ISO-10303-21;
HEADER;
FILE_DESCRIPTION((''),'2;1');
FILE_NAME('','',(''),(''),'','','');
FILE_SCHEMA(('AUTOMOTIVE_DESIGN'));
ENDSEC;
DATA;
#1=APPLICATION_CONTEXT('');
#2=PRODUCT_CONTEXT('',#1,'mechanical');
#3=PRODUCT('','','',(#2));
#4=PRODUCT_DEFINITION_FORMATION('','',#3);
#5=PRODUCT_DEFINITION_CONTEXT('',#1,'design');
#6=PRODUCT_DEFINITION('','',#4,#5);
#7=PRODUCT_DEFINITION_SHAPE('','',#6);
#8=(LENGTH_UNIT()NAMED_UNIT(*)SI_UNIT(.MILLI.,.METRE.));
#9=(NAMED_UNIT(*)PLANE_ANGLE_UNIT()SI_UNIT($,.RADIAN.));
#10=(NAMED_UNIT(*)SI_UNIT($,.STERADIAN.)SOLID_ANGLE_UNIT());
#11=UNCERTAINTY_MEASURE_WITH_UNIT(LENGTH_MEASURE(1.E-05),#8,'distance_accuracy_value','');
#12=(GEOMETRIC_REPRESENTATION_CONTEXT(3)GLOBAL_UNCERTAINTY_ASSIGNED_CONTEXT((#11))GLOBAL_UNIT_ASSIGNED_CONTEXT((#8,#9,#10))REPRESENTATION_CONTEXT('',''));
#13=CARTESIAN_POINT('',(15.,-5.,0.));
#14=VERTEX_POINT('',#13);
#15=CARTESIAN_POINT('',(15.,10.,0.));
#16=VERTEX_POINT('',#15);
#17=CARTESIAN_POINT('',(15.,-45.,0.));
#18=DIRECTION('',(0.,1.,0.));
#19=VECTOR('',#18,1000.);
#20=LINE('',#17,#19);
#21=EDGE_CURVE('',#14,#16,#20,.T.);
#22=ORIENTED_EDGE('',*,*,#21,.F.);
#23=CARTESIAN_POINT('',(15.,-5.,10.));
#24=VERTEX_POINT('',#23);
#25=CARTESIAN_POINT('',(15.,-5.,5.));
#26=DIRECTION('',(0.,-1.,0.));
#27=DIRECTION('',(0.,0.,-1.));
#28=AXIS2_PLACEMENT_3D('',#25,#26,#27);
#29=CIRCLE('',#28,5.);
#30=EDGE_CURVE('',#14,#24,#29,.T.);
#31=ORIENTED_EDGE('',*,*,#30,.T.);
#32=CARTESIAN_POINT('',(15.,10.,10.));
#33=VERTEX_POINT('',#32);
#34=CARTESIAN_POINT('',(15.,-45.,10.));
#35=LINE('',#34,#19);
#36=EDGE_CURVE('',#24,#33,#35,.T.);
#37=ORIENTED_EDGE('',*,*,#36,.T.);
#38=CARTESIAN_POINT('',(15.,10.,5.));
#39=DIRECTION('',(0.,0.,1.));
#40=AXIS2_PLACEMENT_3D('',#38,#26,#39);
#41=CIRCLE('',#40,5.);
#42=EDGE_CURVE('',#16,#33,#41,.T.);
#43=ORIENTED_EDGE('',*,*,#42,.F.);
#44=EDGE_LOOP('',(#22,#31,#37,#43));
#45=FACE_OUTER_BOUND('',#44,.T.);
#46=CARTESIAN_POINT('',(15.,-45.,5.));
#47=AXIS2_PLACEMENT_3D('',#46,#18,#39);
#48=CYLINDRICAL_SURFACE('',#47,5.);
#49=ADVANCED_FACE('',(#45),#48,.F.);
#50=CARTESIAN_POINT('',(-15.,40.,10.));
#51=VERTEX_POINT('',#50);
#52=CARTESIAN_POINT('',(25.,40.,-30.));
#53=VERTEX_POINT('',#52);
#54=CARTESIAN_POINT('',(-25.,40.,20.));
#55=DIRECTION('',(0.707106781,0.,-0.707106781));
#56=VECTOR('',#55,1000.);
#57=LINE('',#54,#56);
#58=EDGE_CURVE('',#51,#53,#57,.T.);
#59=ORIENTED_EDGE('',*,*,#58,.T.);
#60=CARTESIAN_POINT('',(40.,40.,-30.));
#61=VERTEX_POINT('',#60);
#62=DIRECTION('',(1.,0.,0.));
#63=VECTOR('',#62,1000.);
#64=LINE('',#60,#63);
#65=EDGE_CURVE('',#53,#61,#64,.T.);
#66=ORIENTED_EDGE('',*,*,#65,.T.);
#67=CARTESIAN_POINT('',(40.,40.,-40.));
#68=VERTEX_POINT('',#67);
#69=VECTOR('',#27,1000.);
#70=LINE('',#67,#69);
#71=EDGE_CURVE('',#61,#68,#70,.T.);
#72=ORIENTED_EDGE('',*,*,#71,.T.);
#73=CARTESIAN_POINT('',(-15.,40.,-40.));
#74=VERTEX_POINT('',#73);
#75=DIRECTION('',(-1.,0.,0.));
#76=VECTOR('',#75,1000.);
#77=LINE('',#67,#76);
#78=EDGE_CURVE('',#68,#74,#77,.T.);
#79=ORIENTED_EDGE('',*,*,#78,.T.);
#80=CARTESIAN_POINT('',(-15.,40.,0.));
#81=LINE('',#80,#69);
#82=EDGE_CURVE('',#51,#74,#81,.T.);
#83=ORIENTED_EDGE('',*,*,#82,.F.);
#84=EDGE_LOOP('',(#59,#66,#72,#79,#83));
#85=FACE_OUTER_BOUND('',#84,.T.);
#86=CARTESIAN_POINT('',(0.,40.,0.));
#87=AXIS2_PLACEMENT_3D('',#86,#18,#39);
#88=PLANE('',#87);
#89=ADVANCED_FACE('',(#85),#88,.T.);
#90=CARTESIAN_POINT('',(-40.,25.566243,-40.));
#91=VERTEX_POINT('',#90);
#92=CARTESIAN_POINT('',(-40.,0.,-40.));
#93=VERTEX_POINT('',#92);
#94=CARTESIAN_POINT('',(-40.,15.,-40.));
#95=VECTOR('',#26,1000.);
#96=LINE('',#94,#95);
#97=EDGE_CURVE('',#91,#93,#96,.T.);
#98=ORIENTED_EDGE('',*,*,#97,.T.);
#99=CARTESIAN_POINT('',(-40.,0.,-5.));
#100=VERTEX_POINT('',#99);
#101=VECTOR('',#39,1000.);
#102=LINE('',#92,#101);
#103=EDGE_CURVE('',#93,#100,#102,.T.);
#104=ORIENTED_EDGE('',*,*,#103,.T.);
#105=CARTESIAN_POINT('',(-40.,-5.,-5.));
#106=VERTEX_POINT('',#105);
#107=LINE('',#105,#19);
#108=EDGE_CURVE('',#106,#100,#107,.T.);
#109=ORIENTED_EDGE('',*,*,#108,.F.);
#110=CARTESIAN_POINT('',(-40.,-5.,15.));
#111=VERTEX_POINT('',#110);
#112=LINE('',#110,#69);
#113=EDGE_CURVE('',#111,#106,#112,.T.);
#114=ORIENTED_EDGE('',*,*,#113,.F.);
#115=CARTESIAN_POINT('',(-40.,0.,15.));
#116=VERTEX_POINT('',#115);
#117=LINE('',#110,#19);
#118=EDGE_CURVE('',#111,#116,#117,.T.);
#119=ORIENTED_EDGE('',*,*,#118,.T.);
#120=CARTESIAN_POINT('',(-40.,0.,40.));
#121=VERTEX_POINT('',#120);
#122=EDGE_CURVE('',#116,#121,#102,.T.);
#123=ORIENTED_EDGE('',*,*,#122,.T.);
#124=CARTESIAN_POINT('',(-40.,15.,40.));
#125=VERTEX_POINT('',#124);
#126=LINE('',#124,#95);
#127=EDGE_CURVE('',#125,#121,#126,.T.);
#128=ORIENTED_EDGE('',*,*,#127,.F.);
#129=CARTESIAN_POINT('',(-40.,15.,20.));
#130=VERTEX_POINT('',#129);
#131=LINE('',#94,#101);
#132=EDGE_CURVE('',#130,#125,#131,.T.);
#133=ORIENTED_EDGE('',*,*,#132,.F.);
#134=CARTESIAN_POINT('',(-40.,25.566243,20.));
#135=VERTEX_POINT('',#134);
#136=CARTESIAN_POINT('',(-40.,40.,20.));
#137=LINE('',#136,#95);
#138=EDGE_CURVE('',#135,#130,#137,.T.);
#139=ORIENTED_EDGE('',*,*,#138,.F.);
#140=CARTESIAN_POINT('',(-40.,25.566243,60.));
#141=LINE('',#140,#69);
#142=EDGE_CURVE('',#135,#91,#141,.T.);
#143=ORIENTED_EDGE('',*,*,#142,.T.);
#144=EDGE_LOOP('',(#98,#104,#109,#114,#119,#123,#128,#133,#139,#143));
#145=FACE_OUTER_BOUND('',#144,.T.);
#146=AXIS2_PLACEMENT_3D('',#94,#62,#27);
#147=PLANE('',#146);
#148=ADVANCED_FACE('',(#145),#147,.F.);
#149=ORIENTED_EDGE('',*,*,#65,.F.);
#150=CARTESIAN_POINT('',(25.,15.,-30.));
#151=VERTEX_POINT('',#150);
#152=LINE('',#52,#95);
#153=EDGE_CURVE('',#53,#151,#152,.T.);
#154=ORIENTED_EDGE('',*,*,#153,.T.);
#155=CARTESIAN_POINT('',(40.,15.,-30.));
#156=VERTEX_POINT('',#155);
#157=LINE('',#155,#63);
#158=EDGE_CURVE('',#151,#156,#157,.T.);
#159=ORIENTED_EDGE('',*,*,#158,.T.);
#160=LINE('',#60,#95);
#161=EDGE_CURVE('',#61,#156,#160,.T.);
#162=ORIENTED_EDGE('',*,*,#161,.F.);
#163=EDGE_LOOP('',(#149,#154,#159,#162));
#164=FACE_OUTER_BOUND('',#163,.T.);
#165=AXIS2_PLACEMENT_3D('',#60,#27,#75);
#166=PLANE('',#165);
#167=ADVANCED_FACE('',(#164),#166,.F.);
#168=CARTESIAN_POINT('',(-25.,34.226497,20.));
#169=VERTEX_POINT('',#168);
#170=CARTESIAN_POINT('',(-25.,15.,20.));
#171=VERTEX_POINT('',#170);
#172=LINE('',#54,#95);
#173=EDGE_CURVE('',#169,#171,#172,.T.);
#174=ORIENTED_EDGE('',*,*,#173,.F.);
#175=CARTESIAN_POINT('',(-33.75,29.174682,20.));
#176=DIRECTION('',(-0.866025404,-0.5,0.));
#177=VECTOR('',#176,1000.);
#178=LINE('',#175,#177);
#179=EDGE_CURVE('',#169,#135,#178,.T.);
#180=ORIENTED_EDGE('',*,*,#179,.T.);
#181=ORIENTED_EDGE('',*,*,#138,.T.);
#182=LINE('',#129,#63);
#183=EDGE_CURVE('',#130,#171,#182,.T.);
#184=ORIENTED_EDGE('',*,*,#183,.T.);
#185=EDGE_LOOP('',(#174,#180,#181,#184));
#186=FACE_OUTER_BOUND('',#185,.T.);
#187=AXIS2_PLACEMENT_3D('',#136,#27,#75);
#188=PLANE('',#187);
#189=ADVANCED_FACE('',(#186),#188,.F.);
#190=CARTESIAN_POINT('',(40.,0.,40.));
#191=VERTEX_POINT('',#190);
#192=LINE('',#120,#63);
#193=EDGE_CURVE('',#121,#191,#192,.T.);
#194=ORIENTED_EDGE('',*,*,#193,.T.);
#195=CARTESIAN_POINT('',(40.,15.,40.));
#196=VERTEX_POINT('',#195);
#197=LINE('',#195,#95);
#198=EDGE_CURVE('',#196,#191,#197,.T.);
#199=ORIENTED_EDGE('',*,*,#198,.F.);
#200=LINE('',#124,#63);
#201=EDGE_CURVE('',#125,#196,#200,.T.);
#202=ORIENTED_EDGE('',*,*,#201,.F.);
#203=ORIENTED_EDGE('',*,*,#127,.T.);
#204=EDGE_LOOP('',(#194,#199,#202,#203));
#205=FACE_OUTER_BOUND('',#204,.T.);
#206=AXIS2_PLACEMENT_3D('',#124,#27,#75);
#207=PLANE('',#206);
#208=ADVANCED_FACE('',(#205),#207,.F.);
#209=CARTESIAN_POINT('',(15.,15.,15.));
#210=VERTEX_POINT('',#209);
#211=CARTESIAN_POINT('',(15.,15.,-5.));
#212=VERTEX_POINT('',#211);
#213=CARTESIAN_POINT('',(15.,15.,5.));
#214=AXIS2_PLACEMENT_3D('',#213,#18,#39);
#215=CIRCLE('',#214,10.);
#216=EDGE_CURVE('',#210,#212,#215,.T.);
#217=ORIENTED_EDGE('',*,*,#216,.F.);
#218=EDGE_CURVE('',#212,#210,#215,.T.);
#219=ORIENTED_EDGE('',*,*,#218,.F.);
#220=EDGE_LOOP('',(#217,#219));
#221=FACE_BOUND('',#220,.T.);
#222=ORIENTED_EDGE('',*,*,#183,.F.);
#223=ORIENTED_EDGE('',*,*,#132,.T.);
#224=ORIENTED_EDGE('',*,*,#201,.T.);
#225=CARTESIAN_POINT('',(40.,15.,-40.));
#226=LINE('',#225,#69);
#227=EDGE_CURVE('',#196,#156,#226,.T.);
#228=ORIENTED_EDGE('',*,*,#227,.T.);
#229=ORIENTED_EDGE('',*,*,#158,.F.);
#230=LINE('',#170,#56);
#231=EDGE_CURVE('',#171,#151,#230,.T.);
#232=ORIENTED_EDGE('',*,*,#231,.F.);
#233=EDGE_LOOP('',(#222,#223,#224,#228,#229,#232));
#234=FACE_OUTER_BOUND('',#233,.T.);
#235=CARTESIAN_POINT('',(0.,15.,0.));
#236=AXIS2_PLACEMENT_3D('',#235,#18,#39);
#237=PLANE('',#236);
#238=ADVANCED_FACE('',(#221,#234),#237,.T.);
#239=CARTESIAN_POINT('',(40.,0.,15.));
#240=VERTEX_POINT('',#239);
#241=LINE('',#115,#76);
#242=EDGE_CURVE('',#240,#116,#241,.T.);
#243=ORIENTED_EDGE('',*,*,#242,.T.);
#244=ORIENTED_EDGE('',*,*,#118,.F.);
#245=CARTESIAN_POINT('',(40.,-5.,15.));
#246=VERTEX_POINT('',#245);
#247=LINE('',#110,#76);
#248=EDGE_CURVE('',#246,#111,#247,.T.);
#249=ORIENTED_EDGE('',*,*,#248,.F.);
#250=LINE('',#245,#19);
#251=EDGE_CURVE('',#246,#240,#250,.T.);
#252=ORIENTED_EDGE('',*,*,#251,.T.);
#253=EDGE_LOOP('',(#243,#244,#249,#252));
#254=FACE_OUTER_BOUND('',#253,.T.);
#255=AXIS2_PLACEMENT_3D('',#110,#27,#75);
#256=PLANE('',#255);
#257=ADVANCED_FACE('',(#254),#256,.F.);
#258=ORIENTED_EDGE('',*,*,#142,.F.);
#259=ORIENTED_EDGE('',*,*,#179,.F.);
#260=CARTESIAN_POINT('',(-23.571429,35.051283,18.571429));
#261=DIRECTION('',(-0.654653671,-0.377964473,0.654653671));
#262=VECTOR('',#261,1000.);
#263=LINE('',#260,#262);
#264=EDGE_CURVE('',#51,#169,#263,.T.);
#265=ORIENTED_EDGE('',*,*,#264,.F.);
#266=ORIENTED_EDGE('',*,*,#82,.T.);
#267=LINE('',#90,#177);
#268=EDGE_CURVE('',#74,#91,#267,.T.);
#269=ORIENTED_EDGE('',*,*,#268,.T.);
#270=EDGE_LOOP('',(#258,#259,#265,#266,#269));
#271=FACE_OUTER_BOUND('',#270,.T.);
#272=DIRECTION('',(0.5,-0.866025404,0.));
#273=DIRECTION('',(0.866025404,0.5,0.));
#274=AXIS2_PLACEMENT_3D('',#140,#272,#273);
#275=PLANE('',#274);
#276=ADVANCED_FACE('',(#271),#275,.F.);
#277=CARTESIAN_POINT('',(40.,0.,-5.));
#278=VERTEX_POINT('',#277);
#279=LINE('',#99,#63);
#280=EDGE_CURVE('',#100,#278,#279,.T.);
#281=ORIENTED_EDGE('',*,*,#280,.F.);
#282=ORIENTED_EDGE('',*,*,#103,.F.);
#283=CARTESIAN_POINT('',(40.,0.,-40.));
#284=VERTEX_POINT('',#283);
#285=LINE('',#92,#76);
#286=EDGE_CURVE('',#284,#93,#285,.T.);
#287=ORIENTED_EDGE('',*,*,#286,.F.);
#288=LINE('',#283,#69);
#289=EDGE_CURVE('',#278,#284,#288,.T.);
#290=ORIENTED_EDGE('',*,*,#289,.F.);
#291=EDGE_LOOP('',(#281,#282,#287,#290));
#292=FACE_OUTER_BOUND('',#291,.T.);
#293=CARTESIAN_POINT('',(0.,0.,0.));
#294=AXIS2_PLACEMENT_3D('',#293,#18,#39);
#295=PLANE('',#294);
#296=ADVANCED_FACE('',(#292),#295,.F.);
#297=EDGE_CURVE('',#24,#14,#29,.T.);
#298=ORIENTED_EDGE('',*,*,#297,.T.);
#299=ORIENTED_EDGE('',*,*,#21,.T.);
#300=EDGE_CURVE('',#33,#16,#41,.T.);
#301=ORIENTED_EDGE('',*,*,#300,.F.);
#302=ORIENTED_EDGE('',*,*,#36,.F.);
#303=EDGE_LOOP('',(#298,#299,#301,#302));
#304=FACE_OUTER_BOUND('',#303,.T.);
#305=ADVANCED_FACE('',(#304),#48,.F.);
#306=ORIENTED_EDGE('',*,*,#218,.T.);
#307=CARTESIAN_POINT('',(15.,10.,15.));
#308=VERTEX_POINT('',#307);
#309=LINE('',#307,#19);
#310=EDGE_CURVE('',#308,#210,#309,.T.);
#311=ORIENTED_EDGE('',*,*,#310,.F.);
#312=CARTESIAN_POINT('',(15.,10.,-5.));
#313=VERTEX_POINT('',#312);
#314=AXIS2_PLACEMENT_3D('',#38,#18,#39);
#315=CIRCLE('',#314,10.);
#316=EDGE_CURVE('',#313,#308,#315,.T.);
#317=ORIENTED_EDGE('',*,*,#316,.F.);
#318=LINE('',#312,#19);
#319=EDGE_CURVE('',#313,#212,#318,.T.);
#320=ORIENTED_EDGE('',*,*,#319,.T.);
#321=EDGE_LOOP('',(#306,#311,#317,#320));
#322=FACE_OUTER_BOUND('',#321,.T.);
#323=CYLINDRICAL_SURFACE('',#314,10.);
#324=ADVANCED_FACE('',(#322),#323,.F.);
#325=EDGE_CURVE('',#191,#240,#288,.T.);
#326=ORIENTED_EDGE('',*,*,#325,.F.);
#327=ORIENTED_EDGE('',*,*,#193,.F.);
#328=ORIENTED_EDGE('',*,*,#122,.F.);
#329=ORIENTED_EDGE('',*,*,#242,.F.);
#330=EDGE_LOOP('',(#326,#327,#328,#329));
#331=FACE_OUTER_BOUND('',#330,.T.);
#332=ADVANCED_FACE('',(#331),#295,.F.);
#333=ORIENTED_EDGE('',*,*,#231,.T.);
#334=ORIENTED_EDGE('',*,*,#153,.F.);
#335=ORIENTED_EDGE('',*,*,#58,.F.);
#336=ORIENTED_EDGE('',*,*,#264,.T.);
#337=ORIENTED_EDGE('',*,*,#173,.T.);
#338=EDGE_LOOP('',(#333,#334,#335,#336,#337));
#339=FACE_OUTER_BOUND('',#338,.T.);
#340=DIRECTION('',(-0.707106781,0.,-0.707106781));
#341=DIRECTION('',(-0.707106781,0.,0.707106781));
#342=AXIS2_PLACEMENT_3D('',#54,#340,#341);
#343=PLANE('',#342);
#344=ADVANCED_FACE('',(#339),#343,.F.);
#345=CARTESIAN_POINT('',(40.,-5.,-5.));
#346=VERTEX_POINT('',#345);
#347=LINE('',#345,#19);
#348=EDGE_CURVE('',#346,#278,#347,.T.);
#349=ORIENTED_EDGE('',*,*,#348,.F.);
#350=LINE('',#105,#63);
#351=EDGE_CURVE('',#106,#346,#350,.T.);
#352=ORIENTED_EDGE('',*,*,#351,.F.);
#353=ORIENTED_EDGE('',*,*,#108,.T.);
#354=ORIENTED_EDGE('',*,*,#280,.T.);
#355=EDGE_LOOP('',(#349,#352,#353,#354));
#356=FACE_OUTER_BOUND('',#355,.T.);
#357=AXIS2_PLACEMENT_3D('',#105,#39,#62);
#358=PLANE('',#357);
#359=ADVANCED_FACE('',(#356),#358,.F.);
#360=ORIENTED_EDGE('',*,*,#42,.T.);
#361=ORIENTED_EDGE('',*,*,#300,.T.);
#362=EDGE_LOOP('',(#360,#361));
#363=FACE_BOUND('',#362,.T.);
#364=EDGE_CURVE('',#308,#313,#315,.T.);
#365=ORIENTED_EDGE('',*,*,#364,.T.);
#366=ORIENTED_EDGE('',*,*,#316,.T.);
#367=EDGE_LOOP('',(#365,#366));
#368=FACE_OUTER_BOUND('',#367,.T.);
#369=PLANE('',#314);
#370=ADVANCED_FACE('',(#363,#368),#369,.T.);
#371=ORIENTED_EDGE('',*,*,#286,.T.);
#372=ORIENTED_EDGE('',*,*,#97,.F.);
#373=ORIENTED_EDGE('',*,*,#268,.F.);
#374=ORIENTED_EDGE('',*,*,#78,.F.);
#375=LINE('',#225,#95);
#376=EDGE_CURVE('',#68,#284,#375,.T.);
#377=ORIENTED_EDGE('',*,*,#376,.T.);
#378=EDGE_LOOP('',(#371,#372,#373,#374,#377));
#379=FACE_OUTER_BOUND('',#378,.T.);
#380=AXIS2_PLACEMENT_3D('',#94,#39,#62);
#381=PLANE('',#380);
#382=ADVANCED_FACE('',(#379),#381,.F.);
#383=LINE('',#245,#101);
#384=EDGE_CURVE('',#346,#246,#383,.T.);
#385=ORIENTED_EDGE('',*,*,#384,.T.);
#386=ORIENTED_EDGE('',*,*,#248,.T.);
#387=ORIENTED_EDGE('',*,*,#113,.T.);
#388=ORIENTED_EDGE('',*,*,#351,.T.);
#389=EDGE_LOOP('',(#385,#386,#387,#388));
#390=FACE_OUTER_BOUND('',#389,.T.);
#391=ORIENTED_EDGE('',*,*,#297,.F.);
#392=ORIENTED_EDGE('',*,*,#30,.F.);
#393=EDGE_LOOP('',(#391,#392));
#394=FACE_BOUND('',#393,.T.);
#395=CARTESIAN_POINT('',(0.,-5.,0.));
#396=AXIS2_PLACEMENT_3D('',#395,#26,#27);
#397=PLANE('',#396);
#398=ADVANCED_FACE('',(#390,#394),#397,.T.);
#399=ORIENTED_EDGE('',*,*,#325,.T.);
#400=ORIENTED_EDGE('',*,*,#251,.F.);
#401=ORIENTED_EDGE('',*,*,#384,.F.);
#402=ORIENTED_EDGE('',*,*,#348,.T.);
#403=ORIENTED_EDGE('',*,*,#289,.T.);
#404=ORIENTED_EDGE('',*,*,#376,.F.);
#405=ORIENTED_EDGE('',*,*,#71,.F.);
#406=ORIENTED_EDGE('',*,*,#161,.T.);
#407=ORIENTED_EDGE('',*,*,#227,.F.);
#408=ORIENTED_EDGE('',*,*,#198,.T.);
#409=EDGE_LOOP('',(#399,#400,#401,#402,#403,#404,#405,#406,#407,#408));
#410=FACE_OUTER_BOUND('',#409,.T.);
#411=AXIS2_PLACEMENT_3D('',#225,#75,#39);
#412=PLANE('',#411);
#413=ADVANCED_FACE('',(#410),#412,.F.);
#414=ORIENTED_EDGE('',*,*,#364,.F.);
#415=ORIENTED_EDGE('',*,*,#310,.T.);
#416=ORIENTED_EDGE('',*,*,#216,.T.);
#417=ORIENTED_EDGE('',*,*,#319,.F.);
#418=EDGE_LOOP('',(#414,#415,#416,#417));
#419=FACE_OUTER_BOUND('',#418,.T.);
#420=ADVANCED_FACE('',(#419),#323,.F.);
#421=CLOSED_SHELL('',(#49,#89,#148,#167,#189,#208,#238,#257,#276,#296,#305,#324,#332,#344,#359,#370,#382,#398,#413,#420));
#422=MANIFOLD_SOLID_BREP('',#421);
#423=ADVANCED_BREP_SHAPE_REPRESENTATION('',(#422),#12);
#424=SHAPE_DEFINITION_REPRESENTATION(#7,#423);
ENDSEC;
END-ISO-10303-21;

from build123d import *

# Parameters (mm, degrees)
BASE_PLATE_SKETCH_80X80_W          = 80
BASE_PLATE_SKETCH_80X80_H          = 80
BASE_PLATE_80X80X15_DEPTH          = 15
LOCATING_KEY_SKETCH_20X25_W        = 80
LOCATING_KEY_SKETCH_20X25_H        = 20
LOCATING_KEY_20X25X5_DEPTH         = 5
MOUNTING_HOLE_SKETCH_10_R          = 5
MOUNTING_HOLE_10_DEPTH             = 60
COUNTERBORE_SKETCH_20_R            = 10
COUNTERBORE_20X5_DEPTH             = 5
STOP_BLOCK_25_HIGH_DEPTH           = 25
V_STOP_ANGLED_FACE_CUT_30DEG_DEPTH = 100


with BuildPart() as part:
    # Base Plate Sketch 80x80 → Base Plate 80x80x15 (new body)
    with BuildSketch(Plane(origin=(0, 0, 0), x_dir=(1, 0, 0), z_dir=(0, 1, 0))):
        Rectangle(BASE_PLATE_SKETCH_80X80_W, BASE_PLATE_SKETCH_80X80_H)
    extrude(amount=BASE_PLATE_80X80X15_DEPTH)

    # Locating Key Sketch 20x25 → Locating Key 20x25x5 (add)
    with BuildSketch(Plane.XZ):
        with Locations((0, 5)):
            Rectangle(LOCATING_KEY_SKETCH_20X25_W, LOCATING_KEY_SKETCH_20X25_H)
    extrude(amount=LOCATING_KEY_20X25X5_DEPTH)

    # Mounting Hole Sketch Ø10 → Mounting Hole Ø10 (cut)
    with BuildSketch(Plane(origin=(0, 15, 0), x_dir=(1, 0, 0), z_dir=(0, 1, 0))):
        with Locations(Location((15, -5, 0), (0, 0, 270))):
            Circle(MOUNTING_HOLE_SKETCH_10_R)
    extrude(amount=-MOUNTING_HOLE_10_DEPTH, mode=Mode.SUBTRACT)

    # Counterbore Sketch Ø20 → Counterbore Ø20x5 (cut)
    with BuildSketch(Plane(origin=(0, 15, 0), x_dir=(1, 0, 0), z_dir=(0, 1, 0))):
        with Locations(Location((15, -5, 0), (0, 0, 270))):
            Circle(COUNTERBORE_SKETCH_20_R)
    extrude(amount=-COUNTERBORE_20X5_DEPTH, mode=Mode.SUBTRACT)

    # Stop Block Profile Sketch → Stop Block 25 High (add)
    with BuildSketch(Plane(origin=(0, 15, 0), x_dir=(1, 0, 0), z_dir=(0, 1, 0))):
        Polygon((40, 40), (40, 30), (25, 30), (-25, -20), (-40, -20), (-40, 40), align=None)
    extrude(amount=STOP_BLOCK_25_HIGH_DEPTH)

    # V-Stop Angle Sketch 30deg → V-Stop Angled Face Cut 30deg (cut)
    with BuildSketch(Plane(origin=(0, 0, -40), x_dir=(-1, 0, 0), z_dir=(0, 0, -1))):
        Polygon((40, 25.56624327), (15, 40), (40, 40), align=None)
    extrude(amount=-V_STOP_ANGLED_FACE_CUT_30DEG_DEPTH, mode=Mode.SUBTRACT)


solid = part.part
